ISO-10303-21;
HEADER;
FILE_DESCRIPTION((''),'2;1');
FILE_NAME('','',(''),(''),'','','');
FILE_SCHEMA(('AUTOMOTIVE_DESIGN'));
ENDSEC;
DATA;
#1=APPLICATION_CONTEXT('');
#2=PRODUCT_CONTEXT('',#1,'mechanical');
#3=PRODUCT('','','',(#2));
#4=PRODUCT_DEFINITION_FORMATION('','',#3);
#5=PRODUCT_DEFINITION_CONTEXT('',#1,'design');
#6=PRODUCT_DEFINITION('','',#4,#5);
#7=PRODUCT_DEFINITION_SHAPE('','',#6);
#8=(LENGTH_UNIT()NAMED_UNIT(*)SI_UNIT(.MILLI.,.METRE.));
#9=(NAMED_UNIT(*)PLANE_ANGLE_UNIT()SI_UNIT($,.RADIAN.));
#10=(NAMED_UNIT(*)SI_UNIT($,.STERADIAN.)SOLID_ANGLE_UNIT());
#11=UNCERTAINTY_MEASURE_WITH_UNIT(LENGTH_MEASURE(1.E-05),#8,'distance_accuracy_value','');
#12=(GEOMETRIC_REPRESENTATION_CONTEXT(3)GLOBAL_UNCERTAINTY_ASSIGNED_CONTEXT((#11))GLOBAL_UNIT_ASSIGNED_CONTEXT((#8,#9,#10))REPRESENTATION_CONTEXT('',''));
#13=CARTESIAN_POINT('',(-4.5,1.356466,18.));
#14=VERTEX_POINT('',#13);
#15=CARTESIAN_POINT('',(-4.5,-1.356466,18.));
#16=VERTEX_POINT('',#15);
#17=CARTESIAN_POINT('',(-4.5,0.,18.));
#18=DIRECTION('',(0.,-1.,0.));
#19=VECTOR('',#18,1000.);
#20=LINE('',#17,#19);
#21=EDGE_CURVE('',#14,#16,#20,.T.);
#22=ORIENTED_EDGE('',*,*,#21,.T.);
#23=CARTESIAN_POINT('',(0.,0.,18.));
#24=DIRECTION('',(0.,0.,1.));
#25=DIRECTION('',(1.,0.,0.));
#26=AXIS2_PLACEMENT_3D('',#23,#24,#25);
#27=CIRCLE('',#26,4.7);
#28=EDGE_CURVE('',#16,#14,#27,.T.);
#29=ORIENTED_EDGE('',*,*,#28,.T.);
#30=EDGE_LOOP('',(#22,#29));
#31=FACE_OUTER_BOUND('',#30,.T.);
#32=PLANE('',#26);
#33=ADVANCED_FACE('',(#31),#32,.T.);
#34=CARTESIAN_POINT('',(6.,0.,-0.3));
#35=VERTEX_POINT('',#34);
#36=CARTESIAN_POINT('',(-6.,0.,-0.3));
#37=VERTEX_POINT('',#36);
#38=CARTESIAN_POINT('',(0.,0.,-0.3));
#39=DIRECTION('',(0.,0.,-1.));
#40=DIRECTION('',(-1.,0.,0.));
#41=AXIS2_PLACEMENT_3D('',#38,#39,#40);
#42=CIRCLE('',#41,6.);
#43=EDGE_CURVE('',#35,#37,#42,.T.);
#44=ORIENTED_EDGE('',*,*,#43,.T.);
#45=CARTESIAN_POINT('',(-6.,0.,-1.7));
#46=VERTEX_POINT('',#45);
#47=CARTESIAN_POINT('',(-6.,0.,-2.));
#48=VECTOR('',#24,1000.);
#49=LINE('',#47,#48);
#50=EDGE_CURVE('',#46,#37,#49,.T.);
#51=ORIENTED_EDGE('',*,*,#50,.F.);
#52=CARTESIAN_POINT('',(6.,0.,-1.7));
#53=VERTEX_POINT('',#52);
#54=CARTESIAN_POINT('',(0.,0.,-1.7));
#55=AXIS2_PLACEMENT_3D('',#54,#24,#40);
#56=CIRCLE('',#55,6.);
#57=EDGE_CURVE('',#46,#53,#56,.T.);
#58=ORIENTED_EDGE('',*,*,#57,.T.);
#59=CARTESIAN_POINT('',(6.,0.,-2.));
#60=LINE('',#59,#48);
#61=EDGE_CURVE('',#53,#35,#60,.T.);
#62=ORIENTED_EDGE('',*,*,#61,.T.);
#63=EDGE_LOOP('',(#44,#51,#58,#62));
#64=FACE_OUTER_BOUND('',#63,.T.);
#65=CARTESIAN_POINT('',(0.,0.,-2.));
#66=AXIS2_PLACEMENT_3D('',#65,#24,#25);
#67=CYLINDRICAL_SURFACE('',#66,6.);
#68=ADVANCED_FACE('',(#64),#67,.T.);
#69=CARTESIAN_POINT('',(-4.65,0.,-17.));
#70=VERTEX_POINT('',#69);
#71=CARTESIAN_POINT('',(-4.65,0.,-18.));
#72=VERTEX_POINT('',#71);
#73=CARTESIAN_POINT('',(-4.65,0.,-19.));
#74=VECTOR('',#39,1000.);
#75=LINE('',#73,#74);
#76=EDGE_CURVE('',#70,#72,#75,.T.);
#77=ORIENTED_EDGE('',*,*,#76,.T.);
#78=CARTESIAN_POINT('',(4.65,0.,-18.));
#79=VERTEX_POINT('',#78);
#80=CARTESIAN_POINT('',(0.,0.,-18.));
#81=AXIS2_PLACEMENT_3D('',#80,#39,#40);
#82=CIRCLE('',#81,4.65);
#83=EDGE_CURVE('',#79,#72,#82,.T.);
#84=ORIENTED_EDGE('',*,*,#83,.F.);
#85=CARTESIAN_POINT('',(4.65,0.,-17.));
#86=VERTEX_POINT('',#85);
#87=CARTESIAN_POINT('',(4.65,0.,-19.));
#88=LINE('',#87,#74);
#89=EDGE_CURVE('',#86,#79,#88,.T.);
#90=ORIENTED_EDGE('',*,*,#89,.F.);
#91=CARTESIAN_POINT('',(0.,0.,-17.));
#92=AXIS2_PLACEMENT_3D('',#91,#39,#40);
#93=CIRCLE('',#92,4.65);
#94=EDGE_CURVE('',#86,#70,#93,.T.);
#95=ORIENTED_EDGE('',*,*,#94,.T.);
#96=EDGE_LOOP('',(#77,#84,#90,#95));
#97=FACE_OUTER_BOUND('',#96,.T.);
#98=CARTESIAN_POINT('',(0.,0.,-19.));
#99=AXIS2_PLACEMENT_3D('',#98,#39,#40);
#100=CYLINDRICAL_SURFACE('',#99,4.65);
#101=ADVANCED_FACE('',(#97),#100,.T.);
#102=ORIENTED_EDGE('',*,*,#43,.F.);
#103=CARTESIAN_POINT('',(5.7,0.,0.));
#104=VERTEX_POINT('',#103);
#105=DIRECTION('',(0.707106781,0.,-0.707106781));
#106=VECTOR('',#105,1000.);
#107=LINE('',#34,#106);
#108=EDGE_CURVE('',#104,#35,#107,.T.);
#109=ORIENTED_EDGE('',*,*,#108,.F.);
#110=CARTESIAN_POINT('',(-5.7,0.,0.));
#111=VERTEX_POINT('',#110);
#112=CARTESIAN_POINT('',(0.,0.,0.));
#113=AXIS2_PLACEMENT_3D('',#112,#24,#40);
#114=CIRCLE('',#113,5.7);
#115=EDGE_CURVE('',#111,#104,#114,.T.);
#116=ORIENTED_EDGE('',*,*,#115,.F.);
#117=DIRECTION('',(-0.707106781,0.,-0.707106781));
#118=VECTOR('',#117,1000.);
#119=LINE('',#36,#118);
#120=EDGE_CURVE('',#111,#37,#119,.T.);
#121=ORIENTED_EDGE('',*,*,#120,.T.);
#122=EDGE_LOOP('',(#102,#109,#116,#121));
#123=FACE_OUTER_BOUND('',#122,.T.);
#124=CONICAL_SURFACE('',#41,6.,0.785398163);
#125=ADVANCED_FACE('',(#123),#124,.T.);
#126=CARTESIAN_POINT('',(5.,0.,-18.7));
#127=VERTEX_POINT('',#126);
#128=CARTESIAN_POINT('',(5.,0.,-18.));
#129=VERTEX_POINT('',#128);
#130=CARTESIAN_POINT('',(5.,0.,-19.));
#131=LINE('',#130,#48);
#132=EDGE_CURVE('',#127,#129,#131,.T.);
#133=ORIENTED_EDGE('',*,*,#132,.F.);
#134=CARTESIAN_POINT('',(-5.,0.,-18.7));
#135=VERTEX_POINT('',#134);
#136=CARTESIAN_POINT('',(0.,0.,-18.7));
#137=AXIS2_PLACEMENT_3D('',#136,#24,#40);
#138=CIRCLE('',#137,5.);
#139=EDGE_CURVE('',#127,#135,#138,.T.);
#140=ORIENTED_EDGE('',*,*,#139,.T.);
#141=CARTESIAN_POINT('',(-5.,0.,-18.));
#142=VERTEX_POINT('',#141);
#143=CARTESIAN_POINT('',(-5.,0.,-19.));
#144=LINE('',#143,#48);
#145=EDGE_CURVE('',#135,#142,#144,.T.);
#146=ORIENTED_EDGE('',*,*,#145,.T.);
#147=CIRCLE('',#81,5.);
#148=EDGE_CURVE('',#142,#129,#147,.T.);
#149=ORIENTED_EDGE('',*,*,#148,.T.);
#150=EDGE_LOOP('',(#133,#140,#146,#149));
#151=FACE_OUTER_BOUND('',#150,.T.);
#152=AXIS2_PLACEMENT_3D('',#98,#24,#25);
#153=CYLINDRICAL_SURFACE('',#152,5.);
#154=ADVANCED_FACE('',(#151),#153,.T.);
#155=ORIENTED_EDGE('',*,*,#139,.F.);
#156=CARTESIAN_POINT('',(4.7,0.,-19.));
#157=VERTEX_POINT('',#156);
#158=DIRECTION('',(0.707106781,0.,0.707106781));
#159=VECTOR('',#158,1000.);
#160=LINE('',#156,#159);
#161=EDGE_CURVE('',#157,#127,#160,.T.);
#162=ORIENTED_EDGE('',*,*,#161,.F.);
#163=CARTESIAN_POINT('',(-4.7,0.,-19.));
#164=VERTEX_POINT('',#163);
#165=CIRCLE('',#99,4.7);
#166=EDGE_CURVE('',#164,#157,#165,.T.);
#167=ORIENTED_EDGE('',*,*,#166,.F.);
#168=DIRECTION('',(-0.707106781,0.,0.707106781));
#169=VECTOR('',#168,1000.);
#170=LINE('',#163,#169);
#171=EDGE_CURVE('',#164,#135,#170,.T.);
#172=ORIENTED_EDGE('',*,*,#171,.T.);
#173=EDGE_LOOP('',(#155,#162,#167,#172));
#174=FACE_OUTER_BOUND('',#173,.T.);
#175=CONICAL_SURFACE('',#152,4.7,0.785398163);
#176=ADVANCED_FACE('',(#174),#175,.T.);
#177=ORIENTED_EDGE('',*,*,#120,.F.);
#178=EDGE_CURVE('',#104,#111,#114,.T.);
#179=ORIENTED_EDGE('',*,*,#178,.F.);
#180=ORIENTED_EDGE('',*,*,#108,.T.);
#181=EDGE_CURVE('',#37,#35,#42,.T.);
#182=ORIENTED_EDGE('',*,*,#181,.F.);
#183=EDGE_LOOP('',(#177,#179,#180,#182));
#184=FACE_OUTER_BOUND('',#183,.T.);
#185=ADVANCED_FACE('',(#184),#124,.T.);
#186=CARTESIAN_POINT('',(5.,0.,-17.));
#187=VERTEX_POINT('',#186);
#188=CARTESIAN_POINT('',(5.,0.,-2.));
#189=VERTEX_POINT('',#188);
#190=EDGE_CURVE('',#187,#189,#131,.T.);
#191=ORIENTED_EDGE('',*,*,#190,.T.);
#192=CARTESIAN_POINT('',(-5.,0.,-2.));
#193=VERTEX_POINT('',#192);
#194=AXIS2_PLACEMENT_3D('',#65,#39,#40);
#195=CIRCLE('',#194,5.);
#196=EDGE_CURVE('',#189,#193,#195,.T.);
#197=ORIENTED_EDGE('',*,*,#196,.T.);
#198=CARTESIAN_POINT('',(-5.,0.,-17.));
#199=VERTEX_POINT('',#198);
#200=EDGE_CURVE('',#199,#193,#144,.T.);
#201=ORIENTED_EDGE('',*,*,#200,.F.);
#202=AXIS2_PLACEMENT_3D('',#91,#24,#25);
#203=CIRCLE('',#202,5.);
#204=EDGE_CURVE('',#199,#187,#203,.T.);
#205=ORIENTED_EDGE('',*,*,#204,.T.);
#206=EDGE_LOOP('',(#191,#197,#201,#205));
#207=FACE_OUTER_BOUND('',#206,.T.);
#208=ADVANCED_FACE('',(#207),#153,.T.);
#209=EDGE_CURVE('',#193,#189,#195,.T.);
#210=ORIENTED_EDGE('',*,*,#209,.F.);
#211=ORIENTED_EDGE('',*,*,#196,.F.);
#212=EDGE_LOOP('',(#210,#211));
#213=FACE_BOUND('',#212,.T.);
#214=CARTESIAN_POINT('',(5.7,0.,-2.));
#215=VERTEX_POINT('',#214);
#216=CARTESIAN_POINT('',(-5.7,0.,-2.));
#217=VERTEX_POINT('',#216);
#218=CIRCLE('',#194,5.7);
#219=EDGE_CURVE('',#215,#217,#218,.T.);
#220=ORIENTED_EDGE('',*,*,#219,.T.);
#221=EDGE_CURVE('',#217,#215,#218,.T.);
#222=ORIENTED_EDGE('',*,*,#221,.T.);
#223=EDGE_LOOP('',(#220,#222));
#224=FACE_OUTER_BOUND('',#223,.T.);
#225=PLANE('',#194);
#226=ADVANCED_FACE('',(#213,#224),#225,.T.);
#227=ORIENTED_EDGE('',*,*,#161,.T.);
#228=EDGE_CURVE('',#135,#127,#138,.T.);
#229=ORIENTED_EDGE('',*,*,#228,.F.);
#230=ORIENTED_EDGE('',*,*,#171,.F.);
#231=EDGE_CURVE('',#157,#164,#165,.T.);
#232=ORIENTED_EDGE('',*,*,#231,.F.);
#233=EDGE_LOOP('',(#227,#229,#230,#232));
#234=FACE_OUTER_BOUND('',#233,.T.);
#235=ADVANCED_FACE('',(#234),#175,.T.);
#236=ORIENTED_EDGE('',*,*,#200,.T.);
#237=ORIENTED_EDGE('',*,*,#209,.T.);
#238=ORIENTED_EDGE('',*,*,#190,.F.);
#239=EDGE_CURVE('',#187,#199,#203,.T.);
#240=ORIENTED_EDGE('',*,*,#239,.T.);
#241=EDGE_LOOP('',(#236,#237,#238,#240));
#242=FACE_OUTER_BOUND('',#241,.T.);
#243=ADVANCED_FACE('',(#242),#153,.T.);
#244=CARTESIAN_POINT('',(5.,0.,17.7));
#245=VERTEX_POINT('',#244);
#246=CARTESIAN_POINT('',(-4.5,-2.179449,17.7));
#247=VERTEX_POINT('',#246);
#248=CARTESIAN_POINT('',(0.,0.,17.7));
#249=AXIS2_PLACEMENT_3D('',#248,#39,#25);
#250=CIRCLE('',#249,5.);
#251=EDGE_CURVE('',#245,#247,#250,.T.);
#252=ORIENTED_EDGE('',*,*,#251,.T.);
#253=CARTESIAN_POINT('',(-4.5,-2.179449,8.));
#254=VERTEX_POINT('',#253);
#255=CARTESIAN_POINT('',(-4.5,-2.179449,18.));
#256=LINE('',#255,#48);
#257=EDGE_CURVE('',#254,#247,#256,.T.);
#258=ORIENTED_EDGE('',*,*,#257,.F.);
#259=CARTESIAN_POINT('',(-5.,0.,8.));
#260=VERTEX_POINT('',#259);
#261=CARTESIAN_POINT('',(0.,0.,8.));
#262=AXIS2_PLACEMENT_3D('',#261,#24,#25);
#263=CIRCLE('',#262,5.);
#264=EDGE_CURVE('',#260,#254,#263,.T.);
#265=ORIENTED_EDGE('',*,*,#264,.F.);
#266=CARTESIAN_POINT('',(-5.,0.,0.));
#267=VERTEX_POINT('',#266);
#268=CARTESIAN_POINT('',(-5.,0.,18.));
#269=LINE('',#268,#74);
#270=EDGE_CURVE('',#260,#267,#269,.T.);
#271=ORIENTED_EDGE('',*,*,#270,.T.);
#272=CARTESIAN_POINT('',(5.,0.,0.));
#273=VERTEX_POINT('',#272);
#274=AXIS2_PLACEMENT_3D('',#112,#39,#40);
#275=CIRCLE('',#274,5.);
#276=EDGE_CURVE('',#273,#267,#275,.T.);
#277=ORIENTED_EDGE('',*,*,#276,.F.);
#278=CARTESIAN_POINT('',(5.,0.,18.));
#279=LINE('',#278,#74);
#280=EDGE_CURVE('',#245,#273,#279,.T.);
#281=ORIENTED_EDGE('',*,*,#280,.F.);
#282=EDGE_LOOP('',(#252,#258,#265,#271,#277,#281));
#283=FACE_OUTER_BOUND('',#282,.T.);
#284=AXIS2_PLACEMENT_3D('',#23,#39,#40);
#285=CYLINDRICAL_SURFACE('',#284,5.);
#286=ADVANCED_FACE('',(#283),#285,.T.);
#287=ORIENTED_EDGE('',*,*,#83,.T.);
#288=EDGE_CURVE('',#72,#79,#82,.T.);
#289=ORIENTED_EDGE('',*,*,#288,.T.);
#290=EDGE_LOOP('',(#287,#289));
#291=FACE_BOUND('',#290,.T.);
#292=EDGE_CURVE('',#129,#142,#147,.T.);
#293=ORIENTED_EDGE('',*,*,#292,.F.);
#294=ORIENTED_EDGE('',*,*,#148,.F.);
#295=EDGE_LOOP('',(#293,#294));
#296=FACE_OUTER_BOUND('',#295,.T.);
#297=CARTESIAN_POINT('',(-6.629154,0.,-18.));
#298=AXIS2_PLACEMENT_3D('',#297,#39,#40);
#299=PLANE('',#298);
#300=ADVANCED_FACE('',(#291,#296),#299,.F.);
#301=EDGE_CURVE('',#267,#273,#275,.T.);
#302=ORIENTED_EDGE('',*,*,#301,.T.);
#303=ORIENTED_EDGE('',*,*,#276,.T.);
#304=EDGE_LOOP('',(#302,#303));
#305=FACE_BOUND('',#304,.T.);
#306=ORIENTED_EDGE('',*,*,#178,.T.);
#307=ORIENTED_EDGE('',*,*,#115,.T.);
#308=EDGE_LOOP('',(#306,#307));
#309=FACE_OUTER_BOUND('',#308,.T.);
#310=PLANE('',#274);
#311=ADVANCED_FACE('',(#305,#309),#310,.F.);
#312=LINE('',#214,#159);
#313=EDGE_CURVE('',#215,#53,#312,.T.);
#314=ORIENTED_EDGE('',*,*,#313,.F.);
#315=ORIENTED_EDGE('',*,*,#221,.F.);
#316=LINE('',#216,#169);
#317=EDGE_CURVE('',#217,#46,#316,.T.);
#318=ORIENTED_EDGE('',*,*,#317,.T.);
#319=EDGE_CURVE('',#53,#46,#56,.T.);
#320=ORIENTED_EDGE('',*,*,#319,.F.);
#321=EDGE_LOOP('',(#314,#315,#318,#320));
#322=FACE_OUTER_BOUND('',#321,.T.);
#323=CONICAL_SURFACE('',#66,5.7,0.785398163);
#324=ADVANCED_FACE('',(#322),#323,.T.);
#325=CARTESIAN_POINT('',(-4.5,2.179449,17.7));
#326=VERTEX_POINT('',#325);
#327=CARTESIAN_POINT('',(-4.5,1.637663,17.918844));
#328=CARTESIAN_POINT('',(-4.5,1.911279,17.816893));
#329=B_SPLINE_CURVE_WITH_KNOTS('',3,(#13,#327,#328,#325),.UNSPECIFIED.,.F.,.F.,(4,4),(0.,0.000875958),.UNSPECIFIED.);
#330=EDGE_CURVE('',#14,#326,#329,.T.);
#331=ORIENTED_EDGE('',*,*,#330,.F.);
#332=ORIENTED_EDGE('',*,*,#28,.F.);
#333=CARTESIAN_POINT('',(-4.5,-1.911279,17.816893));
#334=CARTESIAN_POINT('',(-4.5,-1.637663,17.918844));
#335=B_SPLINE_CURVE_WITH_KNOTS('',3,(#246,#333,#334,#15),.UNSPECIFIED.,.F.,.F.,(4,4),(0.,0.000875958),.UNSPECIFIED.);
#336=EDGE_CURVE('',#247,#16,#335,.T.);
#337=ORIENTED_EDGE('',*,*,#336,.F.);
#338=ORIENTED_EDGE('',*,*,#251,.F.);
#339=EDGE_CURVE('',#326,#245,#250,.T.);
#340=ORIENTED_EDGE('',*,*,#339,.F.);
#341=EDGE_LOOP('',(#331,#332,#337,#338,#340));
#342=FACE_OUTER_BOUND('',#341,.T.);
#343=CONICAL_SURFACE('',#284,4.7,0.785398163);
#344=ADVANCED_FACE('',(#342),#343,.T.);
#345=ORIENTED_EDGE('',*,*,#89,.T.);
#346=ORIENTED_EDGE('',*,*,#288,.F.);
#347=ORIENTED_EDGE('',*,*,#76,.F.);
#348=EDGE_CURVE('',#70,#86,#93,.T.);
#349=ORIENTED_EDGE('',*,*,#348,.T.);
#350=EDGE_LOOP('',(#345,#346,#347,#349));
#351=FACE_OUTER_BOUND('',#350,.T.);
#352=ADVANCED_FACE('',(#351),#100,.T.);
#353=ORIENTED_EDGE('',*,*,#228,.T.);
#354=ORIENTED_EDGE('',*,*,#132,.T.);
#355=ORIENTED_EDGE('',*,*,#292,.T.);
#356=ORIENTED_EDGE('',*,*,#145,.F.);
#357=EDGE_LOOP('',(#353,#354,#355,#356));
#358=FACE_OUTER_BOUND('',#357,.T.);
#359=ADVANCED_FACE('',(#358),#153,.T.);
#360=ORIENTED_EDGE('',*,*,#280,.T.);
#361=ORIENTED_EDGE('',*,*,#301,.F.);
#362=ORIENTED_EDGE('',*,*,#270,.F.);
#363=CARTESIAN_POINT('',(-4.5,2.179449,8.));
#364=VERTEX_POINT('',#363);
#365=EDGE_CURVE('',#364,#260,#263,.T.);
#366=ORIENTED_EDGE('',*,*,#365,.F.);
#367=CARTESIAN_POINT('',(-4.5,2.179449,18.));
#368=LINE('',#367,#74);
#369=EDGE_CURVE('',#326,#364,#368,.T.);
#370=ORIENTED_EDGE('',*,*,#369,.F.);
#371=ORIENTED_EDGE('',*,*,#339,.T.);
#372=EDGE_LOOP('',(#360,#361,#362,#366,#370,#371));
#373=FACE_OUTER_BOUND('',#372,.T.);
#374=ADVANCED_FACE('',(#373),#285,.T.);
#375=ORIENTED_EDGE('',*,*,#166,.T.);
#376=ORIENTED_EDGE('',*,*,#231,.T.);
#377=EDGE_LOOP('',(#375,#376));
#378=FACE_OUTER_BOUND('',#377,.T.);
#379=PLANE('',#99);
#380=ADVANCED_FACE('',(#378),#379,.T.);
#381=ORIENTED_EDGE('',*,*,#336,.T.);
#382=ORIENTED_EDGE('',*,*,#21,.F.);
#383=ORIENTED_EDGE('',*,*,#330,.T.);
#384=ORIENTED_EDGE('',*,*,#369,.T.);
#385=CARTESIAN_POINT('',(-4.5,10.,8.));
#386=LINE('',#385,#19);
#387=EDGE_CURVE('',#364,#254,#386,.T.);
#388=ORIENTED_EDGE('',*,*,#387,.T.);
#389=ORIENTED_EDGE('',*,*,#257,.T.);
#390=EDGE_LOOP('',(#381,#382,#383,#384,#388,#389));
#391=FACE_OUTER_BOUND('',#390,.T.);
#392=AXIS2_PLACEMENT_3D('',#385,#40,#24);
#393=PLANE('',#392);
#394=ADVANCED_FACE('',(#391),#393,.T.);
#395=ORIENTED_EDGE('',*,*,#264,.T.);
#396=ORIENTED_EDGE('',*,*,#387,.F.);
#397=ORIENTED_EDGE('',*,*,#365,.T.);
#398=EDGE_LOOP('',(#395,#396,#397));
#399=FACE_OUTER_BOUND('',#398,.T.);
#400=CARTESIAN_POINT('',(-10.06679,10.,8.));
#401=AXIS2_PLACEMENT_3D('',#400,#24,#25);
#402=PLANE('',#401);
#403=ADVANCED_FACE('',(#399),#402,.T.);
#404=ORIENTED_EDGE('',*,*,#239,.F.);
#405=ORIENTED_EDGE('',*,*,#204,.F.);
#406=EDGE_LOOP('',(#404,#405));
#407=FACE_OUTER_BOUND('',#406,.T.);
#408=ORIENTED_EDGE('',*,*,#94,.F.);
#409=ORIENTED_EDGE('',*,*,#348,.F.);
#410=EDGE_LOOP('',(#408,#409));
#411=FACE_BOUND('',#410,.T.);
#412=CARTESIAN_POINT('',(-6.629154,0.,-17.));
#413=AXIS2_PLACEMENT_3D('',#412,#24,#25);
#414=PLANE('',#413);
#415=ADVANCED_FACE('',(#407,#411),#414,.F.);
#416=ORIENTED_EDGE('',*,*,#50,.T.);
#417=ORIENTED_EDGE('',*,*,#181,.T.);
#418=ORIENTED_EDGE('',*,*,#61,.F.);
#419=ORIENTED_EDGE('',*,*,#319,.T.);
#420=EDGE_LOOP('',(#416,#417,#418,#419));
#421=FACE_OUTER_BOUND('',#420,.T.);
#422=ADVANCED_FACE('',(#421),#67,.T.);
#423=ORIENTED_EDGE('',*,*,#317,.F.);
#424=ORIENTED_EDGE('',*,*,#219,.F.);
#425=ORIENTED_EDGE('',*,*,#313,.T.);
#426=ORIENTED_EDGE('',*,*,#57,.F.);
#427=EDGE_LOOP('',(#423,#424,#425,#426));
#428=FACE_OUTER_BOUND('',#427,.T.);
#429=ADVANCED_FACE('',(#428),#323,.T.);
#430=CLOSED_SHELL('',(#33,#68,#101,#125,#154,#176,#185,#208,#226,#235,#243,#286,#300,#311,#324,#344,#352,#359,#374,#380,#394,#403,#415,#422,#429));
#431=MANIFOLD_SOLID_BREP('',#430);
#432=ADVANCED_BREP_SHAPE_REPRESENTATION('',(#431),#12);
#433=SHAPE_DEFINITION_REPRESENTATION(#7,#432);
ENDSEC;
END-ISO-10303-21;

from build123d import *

# Parameters (mm, degrees)
SKETCH1_R               = 5
BOSS_EXTRUDE1_DEPTH     = 18
SKETCH2_R               = 6
BOSS_EXTRUDE2_DEPTH     = 2
BOSS_EXTRUDE3_START     = 17
SKETCH3_R               = 5
BOSS_EXTRUDE3_DEPTH     = 17
SKETCH4_W               = 1.979153599
SKETCH4_H               = 1
CUT_EXTRUDE1_DEPTH      = 10
CUT_EXTRUDE1_DEPTH_BACK = 10
SKETCH5_W               = 5.566789872
SKETCH5_H               = 10
CHAMFER1_SIZE           = 0.3


with BuildPart() as part:
    # Sketch1 → Boss-Extrude1 (new body)
    with BuildSketch(Plane.XY):
        Circle(SKETCH1_R)
    extrude(amount=BOSS_EXTRUDE1_DEPTH)

    # Sketch2 → Boss-Extrude2 (add)
    with BuildSketch(Plane(origin=(0, 0, 0), x_dir=(-1, 0, 0), z_dir=(0, 0, -1))):
        Circle(SKETCH2_R)
    extrude(amount=BOSS_EXTRUDE2_DEPTH)

    # Sketch3 → Boss-Extrude3 (add)
    with BuildSketch(Plane(origin=(0, 0, -2), x_dir=(-1, 0, 0), z_dir=(0, 0, -1)).offset(BOSS_EXTRUDE3_START)):
        Circle(SKETCH3_R)
    extrude(amount=-BOSS_EXTRUDE3_DEPTH)

    # Sketch4 → Cut-Revolve1 (revolve, cut)
    with BuildSketch(Plane(origin=(0, 0, 0), x_dir=(1, 0, 0), z_dir=(0, 1, 0))):
        with Locations((-5.6395768, 17.5)):
            Rectangle(SKETCH4_W, SKETCH4_H)
    revolve(axis=Axis((0, 0, -19), (0, 0, 1)), mode=Mode.SUBTRACT)

    # Sketch5 → Cut-Extrude1 (cut, two sides: drawn at the far end of the back side and taken through both)
    with BuildSketch(Plane(origin=(0, 0, 0), x_dir=(1, 0, 0), z_dir=(0, 1, 0)).offset(-CUT_EXTRUDE1_DEPTH_BACK)):
        with Locations((-7.283394936, -13)):
            Rectangle(SKETCH5_W, SKETCH5_H)
    extrude(amount=CUT_EXTRUDE1_DEPTH + CUT_EXTRUDE1_DEPTH_BACK, mode=Mode.SUBTRACT)

    # Chamfer1
    chamfer1_edges = [part.edges().sort_by_distance(p)[0] for p in [
        (5, 0, -19),
        (1.118033989, -4.873397172, 18),
        (6, 0, 0),
        (6, 0, -2),
    ]]
    chamfer(chamfer1_edges, length=CHAMFER1_SIZE)


solid = part.part
